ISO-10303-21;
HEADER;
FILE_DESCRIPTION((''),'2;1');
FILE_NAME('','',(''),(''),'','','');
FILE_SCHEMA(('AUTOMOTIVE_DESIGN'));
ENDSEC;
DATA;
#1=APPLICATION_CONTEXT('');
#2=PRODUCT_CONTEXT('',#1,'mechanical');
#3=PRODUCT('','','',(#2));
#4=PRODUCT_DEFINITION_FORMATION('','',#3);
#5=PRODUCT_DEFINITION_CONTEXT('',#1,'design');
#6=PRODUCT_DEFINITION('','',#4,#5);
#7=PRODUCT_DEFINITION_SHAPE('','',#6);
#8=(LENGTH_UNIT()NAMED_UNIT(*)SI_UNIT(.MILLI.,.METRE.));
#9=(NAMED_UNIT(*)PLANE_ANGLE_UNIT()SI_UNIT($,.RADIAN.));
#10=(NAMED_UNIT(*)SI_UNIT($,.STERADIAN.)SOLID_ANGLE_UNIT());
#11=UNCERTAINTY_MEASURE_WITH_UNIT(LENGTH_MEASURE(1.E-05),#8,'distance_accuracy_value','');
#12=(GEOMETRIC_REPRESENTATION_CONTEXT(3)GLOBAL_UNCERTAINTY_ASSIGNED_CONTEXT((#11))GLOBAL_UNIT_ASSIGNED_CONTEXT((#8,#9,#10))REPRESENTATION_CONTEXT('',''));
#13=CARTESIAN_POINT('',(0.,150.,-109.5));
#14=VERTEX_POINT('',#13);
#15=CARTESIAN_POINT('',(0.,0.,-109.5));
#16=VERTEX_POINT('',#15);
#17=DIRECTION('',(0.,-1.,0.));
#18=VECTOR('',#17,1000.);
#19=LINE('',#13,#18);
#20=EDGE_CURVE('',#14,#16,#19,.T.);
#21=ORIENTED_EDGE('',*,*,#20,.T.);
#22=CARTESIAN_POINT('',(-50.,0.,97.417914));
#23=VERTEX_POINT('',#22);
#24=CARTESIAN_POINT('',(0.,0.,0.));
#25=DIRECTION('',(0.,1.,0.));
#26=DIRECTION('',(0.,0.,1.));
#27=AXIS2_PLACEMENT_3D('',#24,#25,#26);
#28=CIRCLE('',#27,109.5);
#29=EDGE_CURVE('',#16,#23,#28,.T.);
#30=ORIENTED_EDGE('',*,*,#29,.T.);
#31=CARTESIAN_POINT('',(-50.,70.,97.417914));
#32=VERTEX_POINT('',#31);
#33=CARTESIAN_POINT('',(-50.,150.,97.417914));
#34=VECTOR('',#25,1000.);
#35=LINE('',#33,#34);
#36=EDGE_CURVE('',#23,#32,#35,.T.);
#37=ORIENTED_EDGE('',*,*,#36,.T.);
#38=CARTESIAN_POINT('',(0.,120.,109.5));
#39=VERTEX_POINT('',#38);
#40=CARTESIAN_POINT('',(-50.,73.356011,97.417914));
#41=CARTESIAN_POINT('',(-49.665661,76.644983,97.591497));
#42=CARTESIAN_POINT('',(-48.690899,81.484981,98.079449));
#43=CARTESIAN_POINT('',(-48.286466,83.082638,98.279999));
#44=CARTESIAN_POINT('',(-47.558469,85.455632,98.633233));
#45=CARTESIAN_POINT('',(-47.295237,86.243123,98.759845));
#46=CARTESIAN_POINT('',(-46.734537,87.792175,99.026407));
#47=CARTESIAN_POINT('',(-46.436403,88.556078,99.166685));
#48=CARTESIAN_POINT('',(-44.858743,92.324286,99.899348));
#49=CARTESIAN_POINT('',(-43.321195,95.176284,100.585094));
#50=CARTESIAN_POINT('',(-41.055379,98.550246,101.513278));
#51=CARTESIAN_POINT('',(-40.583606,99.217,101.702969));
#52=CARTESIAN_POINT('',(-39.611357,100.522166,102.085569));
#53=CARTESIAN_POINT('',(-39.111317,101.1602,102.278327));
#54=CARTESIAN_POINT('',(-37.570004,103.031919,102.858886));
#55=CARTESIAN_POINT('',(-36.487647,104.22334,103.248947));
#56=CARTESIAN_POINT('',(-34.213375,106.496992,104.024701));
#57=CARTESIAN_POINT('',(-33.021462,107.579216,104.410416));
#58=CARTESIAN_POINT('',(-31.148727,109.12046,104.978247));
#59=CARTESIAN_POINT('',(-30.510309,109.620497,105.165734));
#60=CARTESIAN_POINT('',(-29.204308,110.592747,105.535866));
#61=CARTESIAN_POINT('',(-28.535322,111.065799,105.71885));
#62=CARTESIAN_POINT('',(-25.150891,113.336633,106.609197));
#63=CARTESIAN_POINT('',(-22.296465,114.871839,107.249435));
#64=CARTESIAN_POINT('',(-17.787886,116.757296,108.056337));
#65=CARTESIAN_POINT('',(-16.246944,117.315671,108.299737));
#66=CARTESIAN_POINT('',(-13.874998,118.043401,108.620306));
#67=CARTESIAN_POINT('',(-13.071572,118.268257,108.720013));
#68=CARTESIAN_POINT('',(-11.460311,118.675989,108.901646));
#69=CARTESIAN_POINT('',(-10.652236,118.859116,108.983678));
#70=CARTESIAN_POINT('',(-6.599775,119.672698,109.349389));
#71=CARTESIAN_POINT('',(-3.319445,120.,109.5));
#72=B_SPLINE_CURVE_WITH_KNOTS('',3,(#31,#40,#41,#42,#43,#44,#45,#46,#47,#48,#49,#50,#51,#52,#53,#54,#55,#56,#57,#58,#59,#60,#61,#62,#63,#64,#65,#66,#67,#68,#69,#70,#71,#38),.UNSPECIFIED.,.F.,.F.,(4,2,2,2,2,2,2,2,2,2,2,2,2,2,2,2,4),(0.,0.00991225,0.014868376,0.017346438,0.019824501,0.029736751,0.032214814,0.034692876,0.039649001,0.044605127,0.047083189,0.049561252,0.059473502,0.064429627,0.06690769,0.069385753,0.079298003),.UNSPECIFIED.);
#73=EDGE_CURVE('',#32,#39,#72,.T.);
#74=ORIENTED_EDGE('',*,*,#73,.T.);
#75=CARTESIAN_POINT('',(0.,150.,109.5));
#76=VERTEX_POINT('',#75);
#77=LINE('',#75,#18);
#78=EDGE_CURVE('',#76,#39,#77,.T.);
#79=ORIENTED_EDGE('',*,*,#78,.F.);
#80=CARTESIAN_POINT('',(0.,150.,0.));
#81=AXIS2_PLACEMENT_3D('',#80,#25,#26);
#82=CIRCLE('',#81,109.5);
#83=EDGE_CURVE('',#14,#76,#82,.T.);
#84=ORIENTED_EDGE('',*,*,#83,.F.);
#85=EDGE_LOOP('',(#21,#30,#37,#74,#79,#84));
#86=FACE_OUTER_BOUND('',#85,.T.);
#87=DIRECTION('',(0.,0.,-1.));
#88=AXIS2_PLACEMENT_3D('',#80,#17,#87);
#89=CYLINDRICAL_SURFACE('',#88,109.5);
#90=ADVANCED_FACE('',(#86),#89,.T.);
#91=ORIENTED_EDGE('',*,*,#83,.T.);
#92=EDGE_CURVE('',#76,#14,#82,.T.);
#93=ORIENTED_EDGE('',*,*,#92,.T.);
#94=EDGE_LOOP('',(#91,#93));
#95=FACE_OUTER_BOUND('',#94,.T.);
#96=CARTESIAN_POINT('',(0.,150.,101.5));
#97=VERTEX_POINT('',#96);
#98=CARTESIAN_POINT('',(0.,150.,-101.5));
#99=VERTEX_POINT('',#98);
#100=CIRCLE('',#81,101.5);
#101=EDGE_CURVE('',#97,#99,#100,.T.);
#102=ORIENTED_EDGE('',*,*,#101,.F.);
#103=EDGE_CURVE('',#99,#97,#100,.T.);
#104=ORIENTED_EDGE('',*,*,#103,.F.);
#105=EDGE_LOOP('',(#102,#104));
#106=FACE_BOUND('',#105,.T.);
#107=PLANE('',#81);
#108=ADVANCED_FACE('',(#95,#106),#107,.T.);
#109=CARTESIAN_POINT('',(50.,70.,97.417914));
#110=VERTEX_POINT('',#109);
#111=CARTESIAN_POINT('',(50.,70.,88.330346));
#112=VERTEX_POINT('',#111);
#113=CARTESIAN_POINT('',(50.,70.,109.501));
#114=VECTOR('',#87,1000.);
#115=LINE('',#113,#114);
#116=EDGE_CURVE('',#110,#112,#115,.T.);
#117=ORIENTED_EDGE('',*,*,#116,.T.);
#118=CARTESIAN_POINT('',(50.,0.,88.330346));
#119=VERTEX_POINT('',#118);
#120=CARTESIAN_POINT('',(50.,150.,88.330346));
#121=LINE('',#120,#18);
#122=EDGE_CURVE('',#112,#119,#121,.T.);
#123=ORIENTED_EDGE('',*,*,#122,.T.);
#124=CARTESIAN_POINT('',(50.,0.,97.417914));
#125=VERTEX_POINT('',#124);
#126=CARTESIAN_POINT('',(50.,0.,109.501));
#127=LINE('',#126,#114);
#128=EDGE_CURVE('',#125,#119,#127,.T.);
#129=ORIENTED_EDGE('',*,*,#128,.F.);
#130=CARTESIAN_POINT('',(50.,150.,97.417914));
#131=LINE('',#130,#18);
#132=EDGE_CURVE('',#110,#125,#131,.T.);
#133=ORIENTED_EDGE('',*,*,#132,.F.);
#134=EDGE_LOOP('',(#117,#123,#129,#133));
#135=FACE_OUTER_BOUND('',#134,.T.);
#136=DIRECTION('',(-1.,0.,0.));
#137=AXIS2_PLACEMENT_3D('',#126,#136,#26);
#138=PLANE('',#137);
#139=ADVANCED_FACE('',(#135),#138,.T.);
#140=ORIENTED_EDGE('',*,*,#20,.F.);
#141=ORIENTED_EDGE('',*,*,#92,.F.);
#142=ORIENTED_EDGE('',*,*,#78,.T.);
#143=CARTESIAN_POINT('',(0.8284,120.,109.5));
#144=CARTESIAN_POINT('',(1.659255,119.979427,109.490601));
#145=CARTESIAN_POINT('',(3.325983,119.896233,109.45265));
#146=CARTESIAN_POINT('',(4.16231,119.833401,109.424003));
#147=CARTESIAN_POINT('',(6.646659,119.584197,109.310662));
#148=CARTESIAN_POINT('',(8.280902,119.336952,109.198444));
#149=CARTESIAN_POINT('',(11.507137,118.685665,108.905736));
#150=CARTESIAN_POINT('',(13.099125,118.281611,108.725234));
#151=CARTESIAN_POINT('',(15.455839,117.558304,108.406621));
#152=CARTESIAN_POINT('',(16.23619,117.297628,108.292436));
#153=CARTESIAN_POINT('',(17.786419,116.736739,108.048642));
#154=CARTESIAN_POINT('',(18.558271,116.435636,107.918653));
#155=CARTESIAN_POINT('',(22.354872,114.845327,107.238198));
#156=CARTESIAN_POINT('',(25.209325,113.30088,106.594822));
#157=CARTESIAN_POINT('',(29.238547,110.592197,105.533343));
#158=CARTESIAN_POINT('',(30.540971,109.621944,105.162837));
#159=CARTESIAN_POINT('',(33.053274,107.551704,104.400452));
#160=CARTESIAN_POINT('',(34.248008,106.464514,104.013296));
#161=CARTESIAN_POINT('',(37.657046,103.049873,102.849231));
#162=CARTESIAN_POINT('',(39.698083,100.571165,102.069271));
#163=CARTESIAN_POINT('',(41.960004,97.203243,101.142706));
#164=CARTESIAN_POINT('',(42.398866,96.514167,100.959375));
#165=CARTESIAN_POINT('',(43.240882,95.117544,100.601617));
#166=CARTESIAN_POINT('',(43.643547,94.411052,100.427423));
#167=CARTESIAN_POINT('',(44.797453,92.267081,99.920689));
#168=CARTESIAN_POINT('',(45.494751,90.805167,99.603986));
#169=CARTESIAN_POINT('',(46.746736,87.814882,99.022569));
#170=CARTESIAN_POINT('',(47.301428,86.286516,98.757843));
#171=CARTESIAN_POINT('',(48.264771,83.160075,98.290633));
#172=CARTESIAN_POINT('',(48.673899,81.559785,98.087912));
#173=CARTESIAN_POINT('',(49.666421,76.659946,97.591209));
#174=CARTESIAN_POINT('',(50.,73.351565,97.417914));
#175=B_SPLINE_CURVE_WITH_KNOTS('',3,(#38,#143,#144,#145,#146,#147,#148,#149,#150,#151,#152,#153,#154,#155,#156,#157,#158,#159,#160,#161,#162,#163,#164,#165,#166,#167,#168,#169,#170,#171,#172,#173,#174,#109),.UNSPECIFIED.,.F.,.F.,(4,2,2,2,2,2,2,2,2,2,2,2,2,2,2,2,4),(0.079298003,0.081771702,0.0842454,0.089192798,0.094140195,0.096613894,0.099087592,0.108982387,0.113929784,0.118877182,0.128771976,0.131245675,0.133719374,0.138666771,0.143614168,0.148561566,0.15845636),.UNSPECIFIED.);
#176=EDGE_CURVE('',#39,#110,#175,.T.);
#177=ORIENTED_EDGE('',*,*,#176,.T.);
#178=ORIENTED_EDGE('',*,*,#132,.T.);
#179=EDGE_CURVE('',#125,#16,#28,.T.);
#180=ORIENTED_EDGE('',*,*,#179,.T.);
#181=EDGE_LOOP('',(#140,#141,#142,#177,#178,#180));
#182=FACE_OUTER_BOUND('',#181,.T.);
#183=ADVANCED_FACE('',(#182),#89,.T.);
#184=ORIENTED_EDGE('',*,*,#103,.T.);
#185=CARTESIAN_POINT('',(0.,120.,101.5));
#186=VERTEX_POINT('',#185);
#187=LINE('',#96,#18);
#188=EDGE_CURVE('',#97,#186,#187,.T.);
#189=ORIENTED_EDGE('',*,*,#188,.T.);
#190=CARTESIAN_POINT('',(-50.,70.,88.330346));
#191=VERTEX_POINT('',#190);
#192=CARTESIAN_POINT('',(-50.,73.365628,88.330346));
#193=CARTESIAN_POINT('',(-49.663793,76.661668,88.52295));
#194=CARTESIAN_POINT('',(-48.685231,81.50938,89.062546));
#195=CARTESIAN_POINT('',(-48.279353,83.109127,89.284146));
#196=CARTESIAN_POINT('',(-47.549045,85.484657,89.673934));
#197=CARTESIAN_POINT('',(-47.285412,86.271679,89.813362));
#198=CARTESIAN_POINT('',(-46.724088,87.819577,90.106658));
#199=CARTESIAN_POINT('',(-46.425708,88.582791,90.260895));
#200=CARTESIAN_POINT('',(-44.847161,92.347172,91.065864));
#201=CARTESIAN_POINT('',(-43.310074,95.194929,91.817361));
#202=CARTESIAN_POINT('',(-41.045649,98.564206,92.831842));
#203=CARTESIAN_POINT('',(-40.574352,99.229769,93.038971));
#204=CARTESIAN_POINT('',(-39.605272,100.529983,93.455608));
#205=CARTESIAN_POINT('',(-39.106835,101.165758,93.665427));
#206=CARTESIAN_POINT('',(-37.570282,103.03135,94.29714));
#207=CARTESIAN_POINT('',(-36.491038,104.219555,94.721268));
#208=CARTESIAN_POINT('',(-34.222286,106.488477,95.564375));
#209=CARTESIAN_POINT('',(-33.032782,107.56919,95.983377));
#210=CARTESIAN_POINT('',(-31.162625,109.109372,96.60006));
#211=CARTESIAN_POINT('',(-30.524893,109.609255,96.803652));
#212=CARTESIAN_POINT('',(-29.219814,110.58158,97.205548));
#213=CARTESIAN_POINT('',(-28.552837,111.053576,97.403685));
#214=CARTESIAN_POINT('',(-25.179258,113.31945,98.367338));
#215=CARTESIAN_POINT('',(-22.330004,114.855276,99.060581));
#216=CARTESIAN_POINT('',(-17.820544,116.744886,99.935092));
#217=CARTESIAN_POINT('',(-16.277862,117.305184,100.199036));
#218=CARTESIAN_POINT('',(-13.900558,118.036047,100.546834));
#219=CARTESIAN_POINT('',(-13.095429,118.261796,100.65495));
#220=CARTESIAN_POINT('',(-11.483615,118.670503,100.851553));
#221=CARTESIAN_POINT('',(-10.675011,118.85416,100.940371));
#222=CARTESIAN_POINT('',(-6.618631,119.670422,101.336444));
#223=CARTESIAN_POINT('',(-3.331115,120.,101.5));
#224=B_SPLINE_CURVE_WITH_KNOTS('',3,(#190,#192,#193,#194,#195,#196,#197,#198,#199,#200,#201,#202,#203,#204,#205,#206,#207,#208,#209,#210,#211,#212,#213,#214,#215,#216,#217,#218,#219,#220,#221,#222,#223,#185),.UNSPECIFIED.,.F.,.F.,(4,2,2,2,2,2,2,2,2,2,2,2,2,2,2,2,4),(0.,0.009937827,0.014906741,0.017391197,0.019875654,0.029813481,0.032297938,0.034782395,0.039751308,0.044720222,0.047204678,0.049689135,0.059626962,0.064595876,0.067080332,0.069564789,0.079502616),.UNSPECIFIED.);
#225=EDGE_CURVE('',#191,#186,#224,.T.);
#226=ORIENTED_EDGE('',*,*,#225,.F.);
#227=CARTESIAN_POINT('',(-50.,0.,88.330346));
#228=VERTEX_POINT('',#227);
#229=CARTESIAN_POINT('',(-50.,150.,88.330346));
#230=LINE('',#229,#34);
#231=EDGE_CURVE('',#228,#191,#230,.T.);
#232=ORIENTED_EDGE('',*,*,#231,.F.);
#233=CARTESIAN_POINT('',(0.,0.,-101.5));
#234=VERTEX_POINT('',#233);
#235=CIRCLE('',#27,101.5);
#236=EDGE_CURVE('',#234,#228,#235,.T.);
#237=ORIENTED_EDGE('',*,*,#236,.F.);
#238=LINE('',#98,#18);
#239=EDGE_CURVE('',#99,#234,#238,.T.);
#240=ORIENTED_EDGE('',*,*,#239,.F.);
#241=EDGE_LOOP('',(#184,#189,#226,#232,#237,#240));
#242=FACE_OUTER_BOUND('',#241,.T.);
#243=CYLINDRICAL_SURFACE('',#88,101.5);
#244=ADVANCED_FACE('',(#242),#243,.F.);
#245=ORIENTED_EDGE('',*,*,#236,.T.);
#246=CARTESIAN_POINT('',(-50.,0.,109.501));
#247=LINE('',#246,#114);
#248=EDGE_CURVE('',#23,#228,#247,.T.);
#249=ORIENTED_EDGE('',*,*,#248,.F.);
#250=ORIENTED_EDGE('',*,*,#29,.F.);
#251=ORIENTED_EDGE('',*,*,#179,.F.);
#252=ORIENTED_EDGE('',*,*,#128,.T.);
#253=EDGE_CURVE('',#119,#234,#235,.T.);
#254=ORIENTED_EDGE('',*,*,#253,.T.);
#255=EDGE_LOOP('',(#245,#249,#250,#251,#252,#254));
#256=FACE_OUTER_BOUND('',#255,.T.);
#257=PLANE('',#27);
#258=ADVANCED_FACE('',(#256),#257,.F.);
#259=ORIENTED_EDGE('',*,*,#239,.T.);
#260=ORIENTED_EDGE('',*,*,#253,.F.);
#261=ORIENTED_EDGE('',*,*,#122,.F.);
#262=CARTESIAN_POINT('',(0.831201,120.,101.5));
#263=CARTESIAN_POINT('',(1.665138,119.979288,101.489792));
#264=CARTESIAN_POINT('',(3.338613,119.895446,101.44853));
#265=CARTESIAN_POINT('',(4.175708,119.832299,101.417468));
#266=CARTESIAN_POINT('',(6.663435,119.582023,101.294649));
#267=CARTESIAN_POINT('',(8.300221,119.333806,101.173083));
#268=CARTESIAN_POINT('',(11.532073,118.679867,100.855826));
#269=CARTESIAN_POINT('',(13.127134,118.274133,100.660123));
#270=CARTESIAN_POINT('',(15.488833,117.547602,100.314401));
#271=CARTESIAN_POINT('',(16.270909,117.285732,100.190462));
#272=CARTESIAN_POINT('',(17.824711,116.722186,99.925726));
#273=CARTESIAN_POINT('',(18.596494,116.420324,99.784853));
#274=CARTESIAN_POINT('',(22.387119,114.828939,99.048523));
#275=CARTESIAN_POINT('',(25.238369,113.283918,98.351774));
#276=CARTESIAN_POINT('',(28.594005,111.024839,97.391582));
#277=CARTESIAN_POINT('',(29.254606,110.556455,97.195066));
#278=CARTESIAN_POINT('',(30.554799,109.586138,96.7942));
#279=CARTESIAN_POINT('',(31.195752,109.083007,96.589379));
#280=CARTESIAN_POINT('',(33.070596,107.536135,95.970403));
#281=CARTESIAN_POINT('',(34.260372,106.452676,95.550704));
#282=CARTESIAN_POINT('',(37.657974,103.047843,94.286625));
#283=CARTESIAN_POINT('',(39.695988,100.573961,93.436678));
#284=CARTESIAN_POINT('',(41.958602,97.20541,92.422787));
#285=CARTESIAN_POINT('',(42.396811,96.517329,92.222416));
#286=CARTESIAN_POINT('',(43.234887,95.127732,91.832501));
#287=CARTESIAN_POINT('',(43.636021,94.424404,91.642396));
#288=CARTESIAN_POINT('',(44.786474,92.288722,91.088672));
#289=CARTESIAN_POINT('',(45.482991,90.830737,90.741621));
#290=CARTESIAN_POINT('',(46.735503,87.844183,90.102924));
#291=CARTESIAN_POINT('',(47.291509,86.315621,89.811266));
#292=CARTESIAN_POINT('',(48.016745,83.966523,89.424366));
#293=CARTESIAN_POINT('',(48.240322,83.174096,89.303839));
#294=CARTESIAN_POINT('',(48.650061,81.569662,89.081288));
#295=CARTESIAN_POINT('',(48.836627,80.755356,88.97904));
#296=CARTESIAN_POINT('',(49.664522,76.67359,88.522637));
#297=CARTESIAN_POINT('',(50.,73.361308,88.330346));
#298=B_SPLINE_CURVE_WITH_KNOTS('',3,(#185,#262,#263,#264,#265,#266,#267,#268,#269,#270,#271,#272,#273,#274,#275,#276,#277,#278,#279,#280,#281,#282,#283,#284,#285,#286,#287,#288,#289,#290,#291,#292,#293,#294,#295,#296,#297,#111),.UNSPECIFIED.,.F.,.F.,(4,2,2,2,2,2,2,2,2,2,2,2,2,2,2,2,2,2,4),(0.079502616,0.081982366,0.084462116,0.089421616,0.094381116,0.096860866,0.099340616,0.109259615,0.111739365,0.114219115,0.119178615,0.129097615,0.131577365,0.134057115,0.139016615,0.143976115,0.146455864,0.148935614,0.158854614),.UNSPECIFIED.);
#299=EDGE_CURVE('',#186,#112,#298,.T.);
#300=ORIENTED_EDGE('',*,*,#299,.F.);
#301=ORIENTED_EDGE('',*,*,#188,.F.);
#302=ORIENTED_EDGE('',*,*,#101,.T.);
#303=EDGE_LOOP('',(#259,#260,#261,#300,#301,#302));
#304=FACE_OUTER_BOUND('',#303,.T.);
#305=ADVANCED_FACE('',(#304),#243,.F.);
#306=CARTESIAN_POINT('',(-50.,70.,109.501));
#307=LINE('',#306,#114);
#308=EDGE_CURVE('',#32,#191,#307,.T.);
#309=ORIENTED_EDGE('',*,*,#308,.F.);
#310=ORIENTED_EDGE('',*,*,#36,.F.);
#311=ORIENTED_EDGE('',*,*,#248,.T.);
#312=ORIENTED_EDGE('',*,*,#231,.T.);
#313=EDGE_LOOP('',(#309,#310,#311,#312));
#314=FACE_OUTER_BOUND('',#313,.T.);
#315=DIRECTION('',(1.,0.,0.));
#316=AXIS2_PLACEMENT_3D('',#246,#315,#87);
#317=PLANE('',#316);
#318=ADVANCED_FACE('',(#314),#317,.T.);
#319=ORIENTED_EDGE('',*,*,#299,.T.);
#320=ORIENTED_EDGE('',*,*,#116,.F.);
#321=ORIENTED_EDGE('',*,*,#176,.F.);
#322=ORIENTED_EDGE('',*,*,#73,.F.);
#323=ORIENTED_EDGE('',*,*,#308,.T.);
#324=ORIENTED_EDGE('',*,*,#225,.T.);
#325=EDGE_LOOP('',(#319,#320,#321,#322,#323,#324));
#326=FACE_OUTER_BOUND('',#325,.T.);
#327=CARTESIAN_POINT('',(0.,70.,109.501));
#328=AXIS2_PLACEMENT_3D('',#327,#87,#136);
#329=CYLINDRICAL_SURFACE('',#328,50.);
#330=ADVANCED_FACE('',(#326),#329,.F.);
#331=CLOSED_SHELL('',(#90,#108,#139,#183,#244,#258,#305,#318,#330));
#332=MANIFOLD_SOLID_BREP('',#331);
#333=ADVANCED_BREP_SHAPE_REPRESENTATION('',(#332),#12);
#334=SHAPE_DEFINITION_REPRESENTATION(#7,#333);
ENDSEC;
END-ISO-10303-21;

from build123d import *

# Parameters (mm, degrees)
SKETCH1_R               = 109.5
SKETCH1_R_2             = 101.5
BOSS_EXTRUDE1_DEPTH     = 150
CUT_EXTRUDE1_REACH      = 217.593
CUT_EXTRUDE1_END_RADIUS = 109.5


with BuildPart() as part:
    # Sketch1 → Boss-Extrude1 (new body)
    with BuildSketch(Plane(origin=(0, 0, 0), x_dir=(1, 0, 0), z_dir=(0, 1, 0))):
        with Locations(Location((0, 0, 0), (0, 0, 270))):
            Circle(SKETCH1_R)
        with Locations(Location((0, 0, 0), (0, 0, 270))):
            Circle(SKETCH1_R_2, mode=Mode.SUBTRACT)
    extrude(amount=BOSS_EXTRUDE1_DEPTH)

    # Cut-Extrude1: up to this cylinder (the profile starts inside it)
    cut_extrude1_end = Plane(origin=(0, 35, 0), z_dir=(0, -1, 0)) * Cylinder(CUT_EXTRUDE1_END_RADIUS, 655.186, mode=Mode.PRIVATE)
    # Sketch2 → Cut-Extrude1 (cut, up to the surface)
    with BuildSketch(Plane.XY, mode=Mode.PRIVATE) as cut_extrude1_sk1:
        with BuildLine():
            Line((-50, 0), (-50, 70))
            ThreePointArc((-50, 70), (0, 120), (50, 70))
            Line((50, 70), (50, 0))
            ThreePointArc((50, 0), (0, -50), (-50, 0))
        make_face()
    cut_extrude1_tool1 = extrude(cut_extrude1_sk1.sketch, amount=CUT_EXTRUDE1_REACH, mode=Mode.PRIVATE) & cut_extrude1_end
    add(cut_extrude1_tool1.solids().sort_by_distance((0, 35, 0))[0], mode=Mode.SUBTRACT)


solid = part.part
